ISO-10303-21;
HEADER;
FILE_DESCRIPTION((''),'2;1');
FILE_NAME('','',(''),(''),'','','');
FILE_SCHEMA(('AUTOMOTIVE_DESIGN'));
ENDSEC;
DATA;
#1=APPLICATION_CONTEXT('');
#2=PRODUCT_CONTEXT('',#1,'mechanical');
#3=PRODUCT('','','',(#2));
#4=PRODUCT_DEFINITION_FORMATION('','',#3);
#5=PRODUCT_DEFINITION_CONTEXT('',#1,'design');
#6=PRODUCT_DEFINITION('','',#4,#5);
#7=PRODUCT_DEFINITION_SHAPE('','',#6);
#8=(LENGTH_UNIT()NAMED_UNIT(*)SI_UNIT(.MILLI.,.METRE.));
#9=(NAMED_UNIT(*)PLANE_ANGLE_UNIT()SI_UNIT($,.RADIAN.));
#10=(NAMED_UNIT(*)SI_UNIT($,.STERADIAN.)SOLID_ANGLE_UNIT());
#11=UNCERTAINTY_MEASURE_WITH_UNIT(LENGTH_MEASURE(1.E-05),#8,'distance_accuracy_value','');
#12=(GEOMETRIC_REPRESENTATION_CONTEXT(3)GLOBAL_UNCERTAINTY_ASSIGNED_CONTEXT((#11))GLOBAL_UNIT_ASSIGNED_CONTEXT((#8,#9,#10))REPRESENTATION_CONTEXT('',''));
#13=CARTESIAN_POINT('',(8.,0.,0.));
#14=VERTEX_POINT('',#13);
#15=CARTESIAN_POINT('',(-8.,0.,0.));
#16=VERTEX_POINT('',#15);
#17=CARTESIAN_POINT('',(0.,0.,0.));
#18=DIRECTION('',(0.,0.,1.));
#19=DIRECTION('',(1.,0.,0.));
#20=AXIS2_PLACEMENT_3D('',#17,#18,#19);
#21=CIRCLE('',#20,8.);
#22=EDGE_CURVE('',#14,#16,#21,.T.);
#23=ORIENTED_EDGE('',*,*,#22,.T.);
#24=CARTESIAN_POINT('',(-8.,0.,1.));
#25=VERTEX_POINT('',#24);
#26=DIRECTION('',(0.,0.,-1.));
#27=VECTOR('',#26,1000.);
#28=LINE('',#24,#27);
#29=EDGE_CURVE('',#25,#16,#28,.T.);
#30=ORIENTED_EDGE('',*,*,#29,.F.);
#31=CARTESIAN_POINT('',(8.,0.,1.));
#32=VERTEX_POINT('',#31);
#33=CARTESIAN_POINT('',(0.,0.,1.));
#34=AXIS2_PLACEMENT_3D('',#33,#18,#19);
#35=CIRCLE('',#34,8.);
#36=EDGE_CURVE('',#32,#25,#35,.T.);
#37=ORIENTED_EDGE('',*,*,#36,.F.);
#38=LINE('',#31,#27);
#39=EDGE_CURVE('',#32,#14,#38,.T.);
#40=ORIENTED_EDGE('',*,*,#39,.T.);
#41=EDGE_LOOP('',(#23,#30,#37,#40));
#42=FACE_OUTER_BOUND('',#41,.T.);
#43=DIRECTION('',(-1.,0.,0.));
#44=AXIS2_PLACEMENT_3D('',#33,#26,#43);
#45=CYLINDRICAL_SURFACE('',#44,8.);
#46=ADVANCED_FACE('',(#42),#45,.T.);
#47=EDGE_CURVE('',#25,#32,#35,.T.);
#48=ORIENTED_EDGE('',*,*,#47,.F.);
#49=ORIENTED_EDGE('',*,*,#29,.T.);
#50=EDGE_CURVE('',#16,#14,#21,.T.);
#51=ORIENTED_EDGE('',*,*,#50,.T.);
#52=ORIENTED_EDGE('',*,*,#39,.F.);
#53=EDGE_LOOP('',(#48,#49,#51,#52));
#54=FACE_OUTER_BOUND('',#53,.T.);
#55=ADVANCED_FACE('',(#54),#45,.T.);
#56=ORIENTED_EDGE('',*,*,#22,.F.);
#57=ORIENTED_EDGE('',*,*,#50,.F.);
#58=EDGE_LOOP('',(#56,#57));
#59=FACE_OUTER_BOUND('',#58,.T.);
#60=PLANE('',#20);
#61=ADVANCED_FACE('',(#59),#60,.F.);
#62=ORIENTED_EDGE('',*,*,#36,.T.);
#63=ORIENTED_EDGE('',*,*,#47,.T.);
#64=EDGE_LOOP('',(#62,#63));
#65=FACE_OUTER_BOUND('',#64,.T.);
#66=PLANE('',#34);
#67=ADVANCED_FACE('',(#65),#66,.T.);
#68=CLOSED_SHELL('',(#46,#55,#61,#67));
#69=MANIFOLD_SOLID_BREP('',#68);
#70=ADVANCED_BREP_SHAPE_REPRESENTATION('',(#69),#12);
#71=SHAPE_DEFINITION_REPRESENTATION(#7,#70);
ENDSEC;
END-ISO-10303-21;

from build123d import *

# Parameters (mm, degrees)
SKETCH1_R           = 8
BOSS_EXTRUDE1_DEPTH = 1


with BuildPart() as part:
    # Sketch1 → Boss-Extrude1 (new body)
    with BuildSketch(Plane.XY):
        Circle(SKETCH1_R)
    extrude(amount=BOSS_EXTRUDE1_DEPTH)


solid = part.part
